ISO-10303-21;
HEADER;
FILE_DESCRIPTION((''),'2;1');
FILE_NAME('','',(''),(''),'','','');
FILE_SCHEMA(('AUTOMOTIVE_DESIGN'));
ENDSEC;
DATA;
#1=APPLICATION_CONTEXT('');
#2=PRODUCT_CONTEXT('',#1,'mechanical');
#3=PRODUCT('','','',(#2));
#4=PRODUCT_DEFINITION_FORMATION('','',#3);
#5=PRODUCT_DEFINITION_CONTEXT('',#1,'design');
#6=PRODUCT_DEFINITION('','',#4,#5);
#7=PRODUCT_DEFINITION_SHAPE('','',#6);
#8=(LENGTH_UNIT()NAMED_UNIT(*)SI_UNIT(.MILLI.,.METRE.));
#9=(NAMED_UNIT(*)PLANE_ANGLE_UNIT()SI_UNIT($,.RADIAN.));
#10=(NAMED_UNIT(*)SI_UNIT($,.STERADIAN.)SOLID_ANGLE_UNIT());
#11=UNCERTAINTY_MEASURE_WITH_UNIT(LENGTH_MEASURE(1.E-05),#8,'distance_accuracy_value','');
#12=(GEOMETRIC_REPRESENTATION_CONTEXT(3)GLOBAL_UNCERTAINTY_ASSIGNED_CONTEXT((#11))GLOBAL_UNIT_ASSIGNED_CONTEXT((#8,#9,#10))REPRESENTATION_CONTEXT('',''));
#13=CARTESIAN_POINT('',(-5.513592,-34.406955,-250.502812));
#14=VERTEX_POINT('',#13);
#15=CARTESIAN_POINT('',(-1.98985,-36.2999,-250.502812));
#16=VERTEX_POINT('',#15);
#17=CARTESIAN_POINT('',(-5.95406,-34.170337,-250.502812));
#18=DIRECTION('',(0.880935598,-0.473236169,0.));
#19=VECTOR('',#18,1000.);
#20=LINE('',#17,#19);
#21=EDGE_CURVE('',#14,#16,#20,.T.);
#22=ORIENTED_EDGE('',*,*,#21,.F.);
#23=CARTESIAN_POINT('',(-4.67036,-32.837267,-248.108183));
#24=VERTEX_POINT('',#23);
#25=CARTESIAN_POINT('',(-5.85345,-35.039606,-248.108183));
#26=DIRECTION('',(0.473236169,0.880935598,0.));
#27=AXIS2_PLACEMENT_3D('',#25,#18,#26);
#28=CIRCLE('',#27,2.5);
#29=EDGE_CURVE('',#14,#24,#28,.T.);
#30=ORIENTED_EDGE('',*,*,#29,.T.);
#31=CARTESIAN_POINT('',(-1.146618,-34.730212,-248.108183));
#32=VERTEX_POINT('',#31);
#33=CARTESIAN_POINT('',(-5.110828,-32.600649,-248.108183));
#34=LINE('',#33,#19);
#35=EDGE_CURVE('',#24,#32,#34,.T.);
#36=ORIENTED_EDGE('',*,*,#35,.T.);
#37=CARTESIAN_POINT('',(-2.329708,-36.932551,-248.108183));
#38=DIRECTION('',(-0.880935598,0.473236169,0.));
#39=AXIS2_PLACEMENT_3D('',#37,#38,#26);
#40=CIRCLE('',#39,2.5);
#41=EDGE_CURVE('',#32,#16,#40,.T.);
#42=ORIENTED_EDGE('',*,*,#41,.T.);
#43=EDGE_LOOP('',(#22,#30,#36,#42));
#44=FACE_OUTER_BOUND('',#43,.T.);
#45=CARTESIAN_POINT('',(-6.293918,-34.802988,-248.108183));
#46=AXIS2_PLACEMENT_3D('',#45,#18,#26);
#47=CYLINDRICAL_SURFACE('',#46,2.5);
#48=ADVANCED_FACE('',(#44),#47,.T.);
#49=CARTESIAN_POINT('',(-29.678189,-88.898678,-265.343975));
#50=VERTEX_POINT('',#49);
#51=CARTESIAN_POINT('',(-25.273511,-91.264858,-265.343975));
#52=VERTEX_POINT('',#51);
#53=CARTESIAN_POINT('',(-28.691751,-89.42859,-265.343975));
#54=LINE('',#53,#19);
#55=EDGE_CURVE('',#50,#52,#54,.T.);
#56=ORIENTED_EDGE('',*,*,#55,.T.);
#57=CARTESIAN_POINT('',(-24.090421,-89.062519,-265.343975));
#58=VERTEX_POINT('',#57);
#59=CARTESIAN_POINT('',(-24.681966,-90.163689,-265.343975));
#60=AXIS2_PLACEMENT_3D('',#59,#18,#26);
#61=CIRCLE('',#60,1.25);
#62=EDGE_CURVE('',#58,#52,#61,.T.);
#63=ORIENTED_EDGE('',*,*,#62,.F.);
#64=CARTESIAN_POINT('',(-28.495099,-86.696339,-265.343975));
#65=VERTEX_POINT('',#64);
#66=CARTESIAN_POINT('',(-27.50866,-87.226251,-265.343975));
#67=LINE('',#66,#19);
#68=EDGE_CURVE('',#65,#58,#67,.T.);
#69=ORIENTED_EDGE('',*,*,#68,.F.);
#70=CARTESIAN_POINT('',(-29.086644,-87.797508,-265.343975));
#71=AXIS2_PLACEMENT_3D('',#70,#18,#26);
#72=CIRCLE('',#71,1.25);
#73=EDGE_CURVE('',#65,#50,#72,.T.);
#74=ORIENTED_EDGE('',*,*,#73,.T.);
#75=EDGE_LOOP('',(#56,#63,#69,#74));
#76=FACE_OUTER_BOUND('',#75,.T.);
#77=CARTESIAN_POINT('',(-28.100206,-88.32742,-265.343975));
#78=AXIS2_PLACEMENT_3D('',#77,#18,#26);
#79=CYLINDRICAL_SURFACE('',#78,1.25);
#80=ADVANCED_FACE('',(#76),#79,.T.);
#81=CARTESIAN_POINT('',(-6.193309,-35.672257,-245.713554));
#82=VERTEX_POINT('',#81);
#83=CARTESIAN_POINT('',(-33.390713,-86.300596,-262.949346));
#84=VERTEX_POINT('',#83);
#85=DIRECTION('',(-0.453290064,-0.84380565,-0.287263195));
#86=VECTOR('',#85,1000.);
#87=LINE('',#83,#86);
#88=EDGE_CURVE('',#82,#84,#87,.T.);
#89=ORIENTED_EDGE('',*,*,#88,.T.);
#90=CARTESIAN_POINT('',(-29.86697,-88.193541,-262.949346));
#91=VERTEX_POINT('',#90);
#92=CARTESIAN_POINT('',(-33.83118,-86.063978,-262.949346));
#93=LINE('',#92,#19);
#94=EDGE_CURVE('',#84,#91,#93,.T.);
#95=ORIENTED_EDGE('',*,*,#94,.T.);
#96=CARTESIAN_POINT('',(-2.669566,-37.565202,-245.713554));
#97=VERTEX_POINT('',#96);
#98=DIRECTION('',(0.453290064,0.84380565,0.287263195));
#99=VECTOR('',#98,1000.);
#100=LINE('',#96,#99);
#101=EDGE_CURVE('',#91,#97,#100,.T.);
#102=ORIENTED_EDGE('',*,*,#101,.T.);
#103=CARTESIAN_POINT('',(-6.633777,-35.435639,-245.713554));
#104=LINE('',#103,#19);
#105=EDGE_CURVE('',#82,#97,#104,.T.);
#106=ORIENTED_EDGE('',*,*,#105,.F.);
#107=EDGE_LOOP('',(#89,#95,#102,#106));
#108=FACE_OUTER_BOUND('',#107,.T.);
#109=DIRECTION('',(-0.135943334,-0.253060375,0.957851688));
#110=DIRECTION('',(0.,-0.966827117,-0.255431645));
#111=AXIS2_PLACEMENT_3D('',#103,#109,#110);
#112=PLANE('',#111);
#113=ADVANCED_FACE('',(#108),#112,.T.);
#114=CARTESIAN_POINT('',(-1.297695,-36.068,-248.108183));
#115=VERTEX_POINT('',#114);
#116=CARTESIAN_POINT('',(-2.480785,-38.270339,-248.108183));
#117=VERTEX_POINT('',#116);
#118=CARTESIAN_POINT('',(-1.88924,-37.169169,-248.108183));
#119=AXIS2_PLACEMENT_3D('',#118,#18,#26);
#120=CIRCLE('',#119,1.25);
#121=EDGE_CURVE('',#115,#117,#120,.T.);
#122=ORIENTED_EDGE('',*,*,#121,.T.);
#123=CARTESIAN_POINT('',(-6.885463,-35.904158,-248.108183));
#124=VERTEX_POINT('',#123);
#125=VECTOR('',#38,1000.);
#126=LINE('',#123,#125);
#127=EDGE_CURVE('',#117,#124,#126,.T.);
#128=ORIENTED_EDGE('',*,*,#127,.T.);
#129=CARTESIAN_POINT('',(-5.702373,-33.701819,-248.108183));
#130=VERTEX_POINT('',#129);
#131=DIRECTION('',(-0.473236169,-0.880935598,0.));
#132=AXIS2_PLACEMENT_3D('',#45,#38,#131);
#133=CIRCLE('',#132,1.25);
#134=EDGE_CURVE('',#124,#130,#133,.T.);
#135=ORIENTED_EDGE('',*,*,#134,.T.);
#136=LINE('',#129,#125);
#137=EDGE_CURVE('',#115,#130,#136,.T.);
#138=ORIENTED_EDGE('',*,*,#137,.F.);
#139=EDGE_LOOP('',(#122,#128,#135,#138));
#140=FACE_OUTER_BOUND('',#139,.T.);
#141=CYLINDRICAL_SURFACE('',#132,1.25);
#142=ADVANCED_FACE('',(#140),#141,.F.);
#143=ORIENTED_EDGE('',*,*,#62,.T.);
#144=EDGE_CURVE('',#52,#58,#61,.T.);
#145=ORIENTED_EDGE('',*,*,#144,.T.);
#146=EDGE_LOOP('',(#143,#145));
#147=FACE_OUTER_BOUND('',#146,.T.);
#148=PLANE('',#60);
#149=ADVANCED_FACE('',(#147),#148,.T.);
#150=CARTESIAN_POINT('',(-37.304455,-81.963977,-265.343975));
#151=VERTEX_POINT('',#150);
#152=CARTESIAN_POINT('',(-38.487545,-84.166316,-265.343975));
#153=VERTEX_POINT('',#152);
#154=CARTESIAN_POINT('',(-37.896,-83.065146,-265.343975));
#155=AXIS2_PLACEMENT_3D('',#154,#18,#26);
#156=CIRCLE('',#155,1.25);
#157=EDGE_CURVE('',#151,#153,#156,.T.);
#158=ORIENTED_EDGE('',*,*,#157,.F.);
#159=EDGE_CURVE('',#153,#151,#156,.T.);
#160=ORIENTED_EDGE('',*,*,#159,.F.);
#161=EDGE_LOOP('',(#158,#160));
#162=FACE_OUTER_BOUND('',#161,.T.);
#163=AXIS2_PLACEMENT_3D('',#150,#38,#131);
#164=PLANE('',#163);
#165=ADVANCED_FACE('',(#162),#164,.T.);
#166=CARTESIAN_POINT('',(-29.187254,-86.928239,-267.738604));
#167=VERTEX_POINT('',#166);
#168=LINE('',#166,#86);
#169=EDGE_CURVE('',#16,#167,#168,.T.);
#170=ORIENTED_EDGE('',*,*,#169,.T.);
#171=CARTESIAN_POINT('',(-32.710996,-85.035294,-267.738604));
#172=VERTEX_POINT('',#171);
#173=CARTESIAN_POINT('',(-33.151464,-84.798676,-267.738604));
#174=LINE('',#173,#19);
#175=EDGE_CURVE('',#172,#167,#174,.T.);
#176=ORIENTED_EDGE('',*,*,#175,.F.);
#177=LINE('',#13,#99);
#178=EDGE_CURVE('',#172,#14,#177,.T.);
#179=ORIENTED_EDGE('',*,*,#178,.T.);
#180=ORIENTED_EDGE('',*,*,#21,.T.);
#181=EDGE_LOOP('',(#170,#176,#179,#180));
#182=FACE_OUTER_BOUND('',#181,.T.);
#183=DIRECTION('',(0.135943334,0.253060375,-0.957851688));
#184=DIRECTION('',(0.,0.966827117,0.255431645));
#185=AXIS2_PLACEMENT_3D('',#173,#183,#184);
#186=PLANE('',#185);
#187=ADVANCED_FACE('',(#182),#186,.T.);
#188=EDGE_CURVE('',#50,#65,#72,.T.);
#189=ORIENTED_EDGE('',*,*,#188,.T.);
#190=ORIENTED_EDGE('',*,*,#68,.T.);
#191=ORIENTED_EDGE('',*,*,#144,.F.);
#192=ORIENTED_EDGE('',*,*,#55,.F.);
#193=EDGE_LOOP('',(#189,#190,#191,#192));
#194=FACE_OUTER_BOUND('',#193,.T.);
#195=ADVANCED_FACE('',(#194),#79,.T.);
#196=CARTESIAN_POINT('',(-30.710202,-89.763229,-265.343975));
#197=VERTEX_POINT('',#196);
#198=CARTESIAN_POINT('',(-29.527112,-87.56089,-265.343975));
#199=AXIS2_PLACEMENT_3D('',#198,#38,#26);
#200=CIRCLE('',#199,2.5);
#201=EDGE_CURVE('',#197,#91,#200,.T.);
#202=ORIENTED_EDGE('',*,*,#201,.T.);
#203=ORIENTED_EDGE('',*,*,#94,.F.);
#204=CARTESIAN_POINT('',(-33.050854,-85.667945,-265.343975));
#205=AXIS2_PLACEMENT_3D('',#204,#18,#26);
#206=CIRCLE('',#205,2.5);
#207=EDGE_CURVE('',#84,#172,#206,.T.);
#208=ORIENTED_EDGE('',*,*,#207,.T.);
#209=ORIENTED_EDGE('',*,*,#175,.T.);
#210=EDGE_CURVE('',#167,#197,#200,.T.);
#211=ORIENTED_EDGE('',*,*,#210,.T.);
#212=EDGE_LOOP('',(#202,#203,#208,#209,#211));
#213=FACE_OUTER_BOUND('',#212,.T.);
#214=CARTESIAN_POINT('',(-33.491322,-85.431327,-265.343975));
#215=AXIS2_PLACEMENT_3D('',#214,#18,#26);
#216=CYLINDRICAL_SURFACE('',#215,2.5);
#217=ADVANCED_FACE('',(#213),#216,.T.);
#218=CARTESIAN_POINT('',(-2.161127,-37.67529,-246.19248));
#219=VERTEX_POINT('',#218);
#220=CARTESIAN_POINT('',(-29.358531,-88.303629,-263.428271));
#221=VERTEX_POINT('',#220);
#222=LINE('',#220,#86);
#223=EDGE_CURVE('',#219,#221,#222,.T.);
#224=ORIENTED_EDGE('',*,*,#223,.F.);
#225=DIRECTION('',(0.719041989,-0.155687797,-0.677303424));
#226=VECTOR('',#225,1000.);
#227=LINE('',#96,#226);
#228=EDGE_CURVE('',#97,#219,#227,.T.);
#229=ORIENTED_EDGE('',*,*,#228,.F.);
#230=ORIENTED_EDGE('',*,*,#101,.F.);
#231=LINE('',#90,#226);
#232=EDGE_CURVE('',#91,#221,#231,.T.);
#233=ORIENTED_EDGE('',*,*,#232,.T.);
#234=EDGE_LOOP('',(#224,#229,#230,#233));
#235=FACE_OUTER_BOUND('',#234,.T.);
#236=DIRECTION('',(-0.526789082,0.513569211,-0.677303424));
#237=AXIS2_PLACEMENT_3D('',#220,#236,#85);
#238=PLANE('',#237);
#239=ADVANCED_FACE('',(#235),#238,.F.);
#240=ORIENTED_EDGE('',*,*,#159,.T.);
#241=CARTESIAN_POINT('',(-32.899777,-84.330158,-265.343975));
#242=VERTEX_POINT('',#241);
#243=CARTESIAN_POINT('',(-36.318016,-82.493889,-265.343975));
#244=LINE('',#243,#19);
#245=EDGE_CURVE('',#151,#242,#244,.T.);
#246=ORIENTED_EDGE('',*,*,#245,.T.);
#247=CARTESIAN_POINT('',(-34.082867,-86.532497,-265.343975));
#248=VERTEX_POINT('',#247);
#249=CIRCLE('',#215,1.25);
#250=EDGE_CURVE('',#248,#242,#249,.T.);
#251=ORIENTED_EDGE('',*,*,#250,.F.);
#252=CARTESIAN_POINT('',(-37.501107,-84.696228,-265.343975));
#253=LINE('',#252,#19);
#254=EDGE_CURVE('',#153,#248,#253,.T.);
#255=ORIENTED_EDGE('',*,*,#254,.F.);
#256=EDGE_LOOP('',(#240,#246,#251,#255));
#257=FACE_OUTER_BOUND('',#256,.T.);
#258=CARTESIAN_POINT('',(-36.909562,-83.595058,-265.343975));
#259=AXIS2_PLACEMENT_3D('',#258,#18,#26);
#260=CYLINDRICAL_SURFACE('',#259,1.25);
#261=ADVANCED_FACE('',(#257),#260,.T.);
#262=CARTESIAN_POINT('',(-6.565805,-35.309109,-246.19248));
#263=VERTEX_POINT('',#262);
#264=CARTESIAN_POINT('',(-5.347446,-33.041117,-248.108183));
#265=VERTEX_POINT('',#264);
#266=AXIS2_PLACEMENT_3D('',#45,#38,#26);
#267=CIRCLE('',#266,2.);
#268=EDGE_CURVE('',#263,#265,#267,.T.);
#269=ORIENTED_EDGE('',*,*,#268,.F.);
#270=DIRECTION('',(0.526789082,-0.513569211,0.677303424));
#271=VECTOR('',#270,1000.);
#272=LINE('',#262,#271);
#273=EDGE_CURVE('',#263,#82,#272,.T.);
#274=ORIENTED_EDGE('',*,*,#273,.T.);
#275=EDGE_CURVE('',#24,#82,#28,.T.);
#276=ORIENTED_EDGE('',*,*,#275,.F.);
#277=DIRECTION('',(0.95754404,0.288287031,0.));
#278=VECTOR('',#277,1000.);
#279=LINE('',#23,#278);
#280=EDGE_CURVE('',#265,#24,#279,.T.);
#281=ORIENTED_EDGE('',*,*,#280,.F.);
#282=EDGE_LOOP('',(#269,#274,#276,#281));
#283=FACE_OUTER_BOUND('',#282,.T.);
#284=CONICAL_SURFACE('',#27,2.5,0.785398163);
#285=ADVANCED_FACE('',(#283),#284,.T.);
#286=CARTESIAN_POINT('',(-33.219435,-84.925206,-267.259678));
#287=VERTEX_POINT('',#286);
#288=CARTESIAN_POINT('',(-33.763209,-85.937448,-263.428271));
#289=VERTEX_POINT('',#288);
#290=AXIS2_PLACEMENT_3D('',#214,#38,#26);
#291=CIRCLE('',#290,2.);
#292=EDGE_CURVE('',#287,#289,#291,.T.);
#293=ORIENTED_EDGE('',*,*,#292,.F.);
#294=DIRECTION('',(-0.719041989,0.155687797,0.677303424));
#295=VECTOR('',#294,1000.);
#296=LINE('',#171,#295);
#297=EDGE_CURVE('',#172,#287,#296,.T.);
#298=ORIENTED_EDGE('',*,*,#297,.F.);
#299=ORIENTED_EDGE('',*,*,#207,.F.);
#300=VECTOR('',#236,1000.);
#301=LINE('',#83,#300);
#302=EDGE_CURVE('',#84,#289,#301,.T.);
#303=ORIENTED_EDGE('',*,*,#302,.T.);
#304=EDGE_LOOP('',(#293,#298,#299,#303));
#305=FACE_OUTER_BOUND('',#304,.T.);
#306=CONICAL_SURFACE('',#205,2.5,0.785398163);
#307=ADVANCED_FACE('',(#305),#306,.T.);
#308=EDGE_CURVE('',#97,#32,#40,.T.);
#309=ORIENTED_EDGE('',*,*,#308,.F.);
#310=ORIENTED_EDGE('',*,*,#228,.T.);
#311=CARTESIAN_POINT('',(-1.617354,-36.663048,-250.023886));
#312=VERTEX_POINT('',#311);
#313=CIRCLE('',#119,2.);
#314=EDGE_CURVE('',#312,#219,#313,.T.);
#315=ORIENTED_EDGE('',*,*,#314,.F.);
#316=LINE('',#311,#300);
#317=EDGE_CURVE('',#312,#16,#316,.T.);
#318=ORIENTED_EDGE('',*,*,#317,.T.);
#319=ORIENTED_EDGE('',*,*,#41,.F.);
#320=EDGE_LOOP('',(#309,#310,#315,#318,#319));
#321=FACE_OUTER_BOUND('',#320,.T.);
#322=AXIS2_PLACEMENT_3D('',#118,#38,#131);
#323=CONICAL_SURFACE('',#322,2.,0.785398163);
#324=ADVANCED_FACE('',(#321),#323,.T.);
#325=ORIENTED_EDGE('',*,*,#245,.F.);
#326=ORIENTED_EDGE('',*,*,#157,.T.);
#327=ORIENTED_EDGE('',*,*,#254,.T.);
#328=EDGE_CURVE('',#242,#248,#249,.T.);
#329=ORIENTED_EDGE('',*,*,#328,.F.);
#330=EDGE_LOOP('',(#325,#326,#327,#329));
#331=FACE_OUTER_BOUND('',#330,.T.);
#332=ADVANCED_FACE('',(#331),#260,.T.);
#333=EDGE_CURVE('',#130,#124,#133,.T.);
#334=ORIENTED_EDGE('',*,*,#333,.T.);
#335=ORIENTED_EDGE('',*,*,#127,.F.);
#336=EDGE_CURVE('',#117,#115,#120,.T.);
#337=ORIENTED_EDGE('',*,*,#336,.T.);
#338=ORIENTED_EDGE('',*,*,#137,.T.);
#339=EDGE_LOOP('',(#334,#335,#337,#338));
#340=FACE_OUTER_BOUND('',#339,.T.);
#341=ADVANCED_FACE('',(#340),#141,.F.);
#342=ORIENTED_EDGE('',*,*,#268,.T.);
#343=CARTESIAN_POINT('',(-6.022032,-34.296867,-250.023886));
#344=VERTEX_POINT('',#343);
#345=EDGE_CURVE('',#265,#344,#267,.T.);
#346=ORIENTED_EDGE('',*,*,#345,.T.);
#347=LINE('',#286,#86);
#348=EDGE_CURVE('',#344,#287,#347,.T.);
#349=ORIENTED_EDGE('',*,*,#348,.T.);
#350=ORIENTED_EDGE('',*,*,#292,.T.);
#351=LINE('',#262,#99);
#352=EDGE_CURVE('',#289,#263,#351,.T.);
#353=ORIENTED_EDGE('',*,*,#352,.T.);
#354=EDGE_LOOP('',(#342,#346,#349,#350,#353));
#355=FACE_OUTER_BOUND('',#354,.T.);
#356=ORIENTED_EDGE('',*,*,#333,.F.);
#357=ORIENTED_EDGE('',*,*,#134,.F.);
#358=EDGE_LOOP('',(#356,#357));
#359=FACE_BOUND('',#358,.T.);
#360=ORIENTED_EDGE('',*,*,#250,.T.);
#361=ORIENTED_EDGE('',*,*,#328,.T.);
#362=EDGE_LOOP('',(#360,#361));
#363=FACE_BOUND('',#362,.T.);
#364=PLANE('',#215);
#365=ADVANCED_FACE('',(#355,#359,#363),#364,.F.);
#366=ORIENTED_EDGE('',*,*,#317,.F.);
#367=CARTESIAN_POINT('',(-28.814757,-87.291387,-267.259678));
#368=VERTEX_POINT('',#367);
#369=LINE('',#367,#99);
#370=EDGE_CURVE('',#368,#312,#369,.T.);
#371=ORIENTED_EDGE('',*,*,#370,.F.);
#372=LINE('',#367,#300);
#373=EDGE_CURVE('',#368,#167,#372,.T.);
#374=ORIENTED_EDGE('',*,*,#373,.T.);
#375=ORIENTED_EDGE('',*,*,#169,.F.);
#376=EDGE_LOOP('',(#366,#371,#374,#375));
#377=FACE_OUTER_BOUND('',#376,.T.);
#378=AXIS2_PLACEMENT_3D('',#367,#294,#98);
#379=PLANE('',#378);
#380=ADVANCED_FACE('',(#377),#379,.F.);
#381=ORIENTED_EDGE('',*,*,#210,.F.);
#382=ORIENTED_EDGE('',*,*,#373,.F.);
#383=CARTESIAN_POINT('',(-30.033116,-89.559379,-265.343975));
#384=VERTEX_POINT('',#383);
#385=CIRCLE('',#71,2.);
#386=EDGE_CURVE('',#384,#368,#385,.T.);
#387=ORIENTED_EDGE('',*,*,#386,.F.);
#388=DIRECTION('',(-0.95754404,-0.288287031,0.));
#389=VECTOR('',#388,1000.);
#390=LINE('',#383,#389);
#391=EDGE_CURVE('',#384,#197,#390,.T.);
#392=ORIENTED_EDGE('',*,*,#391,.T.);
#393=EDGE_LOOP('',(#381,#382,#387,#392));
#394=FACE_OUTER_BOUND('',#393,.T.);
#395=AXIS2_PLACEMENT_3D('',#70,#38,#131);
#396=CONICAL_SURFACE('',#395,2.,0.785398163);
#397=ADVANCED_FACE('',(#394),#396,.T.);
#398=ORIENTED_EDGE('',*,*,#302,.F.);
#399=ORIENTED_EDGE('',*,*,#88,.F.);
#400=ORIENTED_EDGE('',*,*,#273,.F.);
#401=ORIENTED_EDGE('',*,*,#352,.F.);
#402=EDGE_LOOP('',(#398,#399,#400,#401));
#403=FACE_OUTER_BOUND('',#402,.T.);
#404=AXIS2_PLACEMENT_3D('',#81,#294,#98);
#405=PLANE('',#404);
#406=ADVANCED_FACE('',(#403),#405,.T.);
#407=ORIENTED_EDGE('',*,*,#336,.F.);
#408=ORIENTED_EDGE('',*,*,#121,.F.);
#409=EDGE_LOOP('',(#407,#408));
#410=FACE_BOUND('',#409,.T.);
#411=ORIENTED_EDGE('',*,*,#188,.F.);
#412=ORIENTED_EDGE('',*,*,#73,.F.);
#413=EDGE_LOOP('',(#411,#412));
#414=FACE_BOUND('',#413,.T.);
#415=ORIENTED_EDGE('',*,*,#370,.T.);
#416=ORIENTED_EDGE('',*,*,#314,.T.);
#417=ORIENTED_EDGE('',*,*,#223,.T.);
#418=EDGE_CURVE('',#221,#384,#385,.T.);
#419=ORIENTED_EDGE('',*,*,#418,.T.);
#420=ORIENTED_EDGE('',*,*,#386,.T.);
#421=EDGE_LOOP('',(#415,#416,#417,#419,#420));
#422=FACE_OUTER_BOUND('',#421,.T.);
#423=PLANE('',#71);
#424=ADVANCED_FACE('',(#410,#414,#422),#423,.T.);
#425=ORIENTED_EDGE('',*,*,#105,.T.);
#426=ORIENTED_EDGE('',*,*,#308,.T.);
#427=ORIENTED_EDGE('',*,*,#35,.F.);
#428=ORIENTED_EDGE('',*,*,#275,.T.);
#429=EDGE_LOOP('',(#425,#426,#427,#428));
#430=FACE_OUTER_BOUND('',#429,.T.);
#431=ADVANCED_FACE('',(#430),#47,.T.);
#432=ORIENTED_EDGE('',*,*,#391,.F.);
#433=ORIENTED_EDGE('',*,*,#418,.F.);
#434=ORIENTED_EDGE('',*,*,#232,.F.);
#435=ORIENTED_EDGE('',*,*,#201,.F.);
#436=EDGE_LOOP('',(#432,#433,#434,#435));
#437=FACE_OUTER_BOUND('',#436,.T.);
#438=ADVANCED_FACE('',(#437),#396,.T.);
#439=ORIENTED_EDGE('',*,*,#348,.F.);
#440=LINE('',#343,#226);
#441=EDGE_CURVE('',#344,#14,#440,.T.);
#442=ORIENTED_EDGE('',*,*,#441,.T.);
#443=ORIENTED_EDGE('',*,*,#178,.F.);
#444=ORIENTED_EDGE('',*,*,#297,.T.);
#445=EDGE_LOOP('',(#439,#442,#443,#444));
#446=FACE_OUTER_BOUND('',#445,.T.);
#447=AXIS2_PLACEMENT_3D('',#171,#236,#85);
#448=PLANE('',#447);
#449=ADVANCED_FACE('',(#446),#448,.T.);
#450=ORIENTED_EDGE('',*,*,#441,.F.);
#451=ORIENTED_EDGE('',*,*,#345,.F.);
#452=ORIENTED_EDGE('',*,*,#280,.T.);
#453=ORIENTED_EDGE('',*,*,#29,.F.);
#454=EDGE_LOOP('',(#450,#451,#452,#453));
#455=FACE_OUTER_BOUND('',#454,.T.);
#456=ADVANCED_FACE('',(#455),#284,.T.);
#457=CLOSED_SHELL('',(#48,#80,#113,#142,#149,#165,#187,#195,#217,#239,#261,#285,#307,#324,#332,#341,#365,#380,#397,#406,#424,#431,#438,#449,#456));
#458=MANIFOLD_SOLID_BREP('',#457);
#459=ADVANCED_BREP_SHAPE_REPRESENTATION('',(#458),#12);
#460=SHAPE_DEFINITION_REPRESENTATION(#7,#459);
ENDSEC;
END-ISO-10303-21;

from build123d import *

# Parameters (mm, degrees)
BOSS_EXTRUDE1_DEPTH            = 5
F_2_5_2_5_DIAMETER_HOLE1_D     = 2.5
F_2_5_2_5_DIAMETER_HOLE1_DEPTH = 31.642263263
CHAMFER1_SIZE                  = 0.5


with BuildPart() as part:
    # Sketch1 → Boss-Extrude1 (new body)
    with BuildSketch(Plane(origin=(14.029336503, -7.536520805, 0), x_dir=(0.4732361692035663, 0.8809355981895235, 0), z_dir=(0.8809355981895235, -0.4732361692035663, -1.915856770880308e-15))):
        with BuildLine():
            Line((-90.390644299, -267.73860401), (-32.919543007, -250.502812288))
            ThreePointArc((-32.919543007, -250.502812288), (-31.243071775, -247.390025079), (-34.355858984, -245.713553847))
            Line((-34.355858984, -245.713553847), (-91.826960276, -262.949345569))
            ThreePointArc((-91.826960276, -262.949345569), (-93.503431508, -266.062132778), (-90.390644299, -267.73860401))
        make_face()
    extrude(amount=-BOSS_EXTRUDE1_DEPTH)

    # Sketch2 → Revolve1 (revolve)
    with BuildSketch(Plane.XY.offset(-265.34397479)):
        Polygon((-37.304454842, -81.963976858), (-37.896000054, -83.065146356), (-33.491322063, -85.431327202), (-32.899776851, -84.330157704), align=None)
    revolve(axis=Axis((-36.90956153, -83.595058405, -265.34397479), (0.880935598189524, -0.47323616920356526, 0)))

    # Sketch3 → Revolve2 (revolve)
    with BuildSketch(Plane.XY.offset(-265.34397479)):
        Polygon((-28.49509886, -86.69633855), (-29.086644072, -87.797508048), (-24.681966081, -90.163688894), (-24.090420869, -89.062519396), align=None)
    revolve(axis=Axis((-28.100205548, -88.327420097, -265.34397479), (0.8809355981895229, -0.4732361692035673, 0)))

    # Ø2.5 (2.5) Diameter Hole1
    with Locations(Plane(origin=(9.624658513, -5.170339959, 0), x_dir=(0, 0, 1), z_dir=(-0.8809355981895236, 0.4732361692035664, 1.9158567708803085e-15))):
        with Locations((-248.108183067, -33.637700995)):
            Hole(F_2_5_2_5_DIAMETER_HOLE1_D / 2, depth=F_2_5_2_5_DIAMETER_HOLE1_DEPTH)

    # Chamfer1
    chamfer1_edges = [part.edges().sort_by_distance(p)[0] for p in [
        (-5.160693088, -32.693474082, -247.390025079),
        (-20.23247849, -60.749808642, -254.331449708),
        (-34.624547222, -87.540841327, -266.062132778),
        (-15.827800499, -63.115989488, -254.331449708),
        (-0.756015097, -35.059654928, -247.390025079),
        (-15.148083829, -61.850687613, -259.120708149),
        (-30.219869231, -89.907022173, -266.062132778),
        (-19.55276182, -59.484506767, -259.120708149),
    ]]
    chamfer(chamfer1_edges, length=CHAMFER1_SIZE)


solid = part.part
